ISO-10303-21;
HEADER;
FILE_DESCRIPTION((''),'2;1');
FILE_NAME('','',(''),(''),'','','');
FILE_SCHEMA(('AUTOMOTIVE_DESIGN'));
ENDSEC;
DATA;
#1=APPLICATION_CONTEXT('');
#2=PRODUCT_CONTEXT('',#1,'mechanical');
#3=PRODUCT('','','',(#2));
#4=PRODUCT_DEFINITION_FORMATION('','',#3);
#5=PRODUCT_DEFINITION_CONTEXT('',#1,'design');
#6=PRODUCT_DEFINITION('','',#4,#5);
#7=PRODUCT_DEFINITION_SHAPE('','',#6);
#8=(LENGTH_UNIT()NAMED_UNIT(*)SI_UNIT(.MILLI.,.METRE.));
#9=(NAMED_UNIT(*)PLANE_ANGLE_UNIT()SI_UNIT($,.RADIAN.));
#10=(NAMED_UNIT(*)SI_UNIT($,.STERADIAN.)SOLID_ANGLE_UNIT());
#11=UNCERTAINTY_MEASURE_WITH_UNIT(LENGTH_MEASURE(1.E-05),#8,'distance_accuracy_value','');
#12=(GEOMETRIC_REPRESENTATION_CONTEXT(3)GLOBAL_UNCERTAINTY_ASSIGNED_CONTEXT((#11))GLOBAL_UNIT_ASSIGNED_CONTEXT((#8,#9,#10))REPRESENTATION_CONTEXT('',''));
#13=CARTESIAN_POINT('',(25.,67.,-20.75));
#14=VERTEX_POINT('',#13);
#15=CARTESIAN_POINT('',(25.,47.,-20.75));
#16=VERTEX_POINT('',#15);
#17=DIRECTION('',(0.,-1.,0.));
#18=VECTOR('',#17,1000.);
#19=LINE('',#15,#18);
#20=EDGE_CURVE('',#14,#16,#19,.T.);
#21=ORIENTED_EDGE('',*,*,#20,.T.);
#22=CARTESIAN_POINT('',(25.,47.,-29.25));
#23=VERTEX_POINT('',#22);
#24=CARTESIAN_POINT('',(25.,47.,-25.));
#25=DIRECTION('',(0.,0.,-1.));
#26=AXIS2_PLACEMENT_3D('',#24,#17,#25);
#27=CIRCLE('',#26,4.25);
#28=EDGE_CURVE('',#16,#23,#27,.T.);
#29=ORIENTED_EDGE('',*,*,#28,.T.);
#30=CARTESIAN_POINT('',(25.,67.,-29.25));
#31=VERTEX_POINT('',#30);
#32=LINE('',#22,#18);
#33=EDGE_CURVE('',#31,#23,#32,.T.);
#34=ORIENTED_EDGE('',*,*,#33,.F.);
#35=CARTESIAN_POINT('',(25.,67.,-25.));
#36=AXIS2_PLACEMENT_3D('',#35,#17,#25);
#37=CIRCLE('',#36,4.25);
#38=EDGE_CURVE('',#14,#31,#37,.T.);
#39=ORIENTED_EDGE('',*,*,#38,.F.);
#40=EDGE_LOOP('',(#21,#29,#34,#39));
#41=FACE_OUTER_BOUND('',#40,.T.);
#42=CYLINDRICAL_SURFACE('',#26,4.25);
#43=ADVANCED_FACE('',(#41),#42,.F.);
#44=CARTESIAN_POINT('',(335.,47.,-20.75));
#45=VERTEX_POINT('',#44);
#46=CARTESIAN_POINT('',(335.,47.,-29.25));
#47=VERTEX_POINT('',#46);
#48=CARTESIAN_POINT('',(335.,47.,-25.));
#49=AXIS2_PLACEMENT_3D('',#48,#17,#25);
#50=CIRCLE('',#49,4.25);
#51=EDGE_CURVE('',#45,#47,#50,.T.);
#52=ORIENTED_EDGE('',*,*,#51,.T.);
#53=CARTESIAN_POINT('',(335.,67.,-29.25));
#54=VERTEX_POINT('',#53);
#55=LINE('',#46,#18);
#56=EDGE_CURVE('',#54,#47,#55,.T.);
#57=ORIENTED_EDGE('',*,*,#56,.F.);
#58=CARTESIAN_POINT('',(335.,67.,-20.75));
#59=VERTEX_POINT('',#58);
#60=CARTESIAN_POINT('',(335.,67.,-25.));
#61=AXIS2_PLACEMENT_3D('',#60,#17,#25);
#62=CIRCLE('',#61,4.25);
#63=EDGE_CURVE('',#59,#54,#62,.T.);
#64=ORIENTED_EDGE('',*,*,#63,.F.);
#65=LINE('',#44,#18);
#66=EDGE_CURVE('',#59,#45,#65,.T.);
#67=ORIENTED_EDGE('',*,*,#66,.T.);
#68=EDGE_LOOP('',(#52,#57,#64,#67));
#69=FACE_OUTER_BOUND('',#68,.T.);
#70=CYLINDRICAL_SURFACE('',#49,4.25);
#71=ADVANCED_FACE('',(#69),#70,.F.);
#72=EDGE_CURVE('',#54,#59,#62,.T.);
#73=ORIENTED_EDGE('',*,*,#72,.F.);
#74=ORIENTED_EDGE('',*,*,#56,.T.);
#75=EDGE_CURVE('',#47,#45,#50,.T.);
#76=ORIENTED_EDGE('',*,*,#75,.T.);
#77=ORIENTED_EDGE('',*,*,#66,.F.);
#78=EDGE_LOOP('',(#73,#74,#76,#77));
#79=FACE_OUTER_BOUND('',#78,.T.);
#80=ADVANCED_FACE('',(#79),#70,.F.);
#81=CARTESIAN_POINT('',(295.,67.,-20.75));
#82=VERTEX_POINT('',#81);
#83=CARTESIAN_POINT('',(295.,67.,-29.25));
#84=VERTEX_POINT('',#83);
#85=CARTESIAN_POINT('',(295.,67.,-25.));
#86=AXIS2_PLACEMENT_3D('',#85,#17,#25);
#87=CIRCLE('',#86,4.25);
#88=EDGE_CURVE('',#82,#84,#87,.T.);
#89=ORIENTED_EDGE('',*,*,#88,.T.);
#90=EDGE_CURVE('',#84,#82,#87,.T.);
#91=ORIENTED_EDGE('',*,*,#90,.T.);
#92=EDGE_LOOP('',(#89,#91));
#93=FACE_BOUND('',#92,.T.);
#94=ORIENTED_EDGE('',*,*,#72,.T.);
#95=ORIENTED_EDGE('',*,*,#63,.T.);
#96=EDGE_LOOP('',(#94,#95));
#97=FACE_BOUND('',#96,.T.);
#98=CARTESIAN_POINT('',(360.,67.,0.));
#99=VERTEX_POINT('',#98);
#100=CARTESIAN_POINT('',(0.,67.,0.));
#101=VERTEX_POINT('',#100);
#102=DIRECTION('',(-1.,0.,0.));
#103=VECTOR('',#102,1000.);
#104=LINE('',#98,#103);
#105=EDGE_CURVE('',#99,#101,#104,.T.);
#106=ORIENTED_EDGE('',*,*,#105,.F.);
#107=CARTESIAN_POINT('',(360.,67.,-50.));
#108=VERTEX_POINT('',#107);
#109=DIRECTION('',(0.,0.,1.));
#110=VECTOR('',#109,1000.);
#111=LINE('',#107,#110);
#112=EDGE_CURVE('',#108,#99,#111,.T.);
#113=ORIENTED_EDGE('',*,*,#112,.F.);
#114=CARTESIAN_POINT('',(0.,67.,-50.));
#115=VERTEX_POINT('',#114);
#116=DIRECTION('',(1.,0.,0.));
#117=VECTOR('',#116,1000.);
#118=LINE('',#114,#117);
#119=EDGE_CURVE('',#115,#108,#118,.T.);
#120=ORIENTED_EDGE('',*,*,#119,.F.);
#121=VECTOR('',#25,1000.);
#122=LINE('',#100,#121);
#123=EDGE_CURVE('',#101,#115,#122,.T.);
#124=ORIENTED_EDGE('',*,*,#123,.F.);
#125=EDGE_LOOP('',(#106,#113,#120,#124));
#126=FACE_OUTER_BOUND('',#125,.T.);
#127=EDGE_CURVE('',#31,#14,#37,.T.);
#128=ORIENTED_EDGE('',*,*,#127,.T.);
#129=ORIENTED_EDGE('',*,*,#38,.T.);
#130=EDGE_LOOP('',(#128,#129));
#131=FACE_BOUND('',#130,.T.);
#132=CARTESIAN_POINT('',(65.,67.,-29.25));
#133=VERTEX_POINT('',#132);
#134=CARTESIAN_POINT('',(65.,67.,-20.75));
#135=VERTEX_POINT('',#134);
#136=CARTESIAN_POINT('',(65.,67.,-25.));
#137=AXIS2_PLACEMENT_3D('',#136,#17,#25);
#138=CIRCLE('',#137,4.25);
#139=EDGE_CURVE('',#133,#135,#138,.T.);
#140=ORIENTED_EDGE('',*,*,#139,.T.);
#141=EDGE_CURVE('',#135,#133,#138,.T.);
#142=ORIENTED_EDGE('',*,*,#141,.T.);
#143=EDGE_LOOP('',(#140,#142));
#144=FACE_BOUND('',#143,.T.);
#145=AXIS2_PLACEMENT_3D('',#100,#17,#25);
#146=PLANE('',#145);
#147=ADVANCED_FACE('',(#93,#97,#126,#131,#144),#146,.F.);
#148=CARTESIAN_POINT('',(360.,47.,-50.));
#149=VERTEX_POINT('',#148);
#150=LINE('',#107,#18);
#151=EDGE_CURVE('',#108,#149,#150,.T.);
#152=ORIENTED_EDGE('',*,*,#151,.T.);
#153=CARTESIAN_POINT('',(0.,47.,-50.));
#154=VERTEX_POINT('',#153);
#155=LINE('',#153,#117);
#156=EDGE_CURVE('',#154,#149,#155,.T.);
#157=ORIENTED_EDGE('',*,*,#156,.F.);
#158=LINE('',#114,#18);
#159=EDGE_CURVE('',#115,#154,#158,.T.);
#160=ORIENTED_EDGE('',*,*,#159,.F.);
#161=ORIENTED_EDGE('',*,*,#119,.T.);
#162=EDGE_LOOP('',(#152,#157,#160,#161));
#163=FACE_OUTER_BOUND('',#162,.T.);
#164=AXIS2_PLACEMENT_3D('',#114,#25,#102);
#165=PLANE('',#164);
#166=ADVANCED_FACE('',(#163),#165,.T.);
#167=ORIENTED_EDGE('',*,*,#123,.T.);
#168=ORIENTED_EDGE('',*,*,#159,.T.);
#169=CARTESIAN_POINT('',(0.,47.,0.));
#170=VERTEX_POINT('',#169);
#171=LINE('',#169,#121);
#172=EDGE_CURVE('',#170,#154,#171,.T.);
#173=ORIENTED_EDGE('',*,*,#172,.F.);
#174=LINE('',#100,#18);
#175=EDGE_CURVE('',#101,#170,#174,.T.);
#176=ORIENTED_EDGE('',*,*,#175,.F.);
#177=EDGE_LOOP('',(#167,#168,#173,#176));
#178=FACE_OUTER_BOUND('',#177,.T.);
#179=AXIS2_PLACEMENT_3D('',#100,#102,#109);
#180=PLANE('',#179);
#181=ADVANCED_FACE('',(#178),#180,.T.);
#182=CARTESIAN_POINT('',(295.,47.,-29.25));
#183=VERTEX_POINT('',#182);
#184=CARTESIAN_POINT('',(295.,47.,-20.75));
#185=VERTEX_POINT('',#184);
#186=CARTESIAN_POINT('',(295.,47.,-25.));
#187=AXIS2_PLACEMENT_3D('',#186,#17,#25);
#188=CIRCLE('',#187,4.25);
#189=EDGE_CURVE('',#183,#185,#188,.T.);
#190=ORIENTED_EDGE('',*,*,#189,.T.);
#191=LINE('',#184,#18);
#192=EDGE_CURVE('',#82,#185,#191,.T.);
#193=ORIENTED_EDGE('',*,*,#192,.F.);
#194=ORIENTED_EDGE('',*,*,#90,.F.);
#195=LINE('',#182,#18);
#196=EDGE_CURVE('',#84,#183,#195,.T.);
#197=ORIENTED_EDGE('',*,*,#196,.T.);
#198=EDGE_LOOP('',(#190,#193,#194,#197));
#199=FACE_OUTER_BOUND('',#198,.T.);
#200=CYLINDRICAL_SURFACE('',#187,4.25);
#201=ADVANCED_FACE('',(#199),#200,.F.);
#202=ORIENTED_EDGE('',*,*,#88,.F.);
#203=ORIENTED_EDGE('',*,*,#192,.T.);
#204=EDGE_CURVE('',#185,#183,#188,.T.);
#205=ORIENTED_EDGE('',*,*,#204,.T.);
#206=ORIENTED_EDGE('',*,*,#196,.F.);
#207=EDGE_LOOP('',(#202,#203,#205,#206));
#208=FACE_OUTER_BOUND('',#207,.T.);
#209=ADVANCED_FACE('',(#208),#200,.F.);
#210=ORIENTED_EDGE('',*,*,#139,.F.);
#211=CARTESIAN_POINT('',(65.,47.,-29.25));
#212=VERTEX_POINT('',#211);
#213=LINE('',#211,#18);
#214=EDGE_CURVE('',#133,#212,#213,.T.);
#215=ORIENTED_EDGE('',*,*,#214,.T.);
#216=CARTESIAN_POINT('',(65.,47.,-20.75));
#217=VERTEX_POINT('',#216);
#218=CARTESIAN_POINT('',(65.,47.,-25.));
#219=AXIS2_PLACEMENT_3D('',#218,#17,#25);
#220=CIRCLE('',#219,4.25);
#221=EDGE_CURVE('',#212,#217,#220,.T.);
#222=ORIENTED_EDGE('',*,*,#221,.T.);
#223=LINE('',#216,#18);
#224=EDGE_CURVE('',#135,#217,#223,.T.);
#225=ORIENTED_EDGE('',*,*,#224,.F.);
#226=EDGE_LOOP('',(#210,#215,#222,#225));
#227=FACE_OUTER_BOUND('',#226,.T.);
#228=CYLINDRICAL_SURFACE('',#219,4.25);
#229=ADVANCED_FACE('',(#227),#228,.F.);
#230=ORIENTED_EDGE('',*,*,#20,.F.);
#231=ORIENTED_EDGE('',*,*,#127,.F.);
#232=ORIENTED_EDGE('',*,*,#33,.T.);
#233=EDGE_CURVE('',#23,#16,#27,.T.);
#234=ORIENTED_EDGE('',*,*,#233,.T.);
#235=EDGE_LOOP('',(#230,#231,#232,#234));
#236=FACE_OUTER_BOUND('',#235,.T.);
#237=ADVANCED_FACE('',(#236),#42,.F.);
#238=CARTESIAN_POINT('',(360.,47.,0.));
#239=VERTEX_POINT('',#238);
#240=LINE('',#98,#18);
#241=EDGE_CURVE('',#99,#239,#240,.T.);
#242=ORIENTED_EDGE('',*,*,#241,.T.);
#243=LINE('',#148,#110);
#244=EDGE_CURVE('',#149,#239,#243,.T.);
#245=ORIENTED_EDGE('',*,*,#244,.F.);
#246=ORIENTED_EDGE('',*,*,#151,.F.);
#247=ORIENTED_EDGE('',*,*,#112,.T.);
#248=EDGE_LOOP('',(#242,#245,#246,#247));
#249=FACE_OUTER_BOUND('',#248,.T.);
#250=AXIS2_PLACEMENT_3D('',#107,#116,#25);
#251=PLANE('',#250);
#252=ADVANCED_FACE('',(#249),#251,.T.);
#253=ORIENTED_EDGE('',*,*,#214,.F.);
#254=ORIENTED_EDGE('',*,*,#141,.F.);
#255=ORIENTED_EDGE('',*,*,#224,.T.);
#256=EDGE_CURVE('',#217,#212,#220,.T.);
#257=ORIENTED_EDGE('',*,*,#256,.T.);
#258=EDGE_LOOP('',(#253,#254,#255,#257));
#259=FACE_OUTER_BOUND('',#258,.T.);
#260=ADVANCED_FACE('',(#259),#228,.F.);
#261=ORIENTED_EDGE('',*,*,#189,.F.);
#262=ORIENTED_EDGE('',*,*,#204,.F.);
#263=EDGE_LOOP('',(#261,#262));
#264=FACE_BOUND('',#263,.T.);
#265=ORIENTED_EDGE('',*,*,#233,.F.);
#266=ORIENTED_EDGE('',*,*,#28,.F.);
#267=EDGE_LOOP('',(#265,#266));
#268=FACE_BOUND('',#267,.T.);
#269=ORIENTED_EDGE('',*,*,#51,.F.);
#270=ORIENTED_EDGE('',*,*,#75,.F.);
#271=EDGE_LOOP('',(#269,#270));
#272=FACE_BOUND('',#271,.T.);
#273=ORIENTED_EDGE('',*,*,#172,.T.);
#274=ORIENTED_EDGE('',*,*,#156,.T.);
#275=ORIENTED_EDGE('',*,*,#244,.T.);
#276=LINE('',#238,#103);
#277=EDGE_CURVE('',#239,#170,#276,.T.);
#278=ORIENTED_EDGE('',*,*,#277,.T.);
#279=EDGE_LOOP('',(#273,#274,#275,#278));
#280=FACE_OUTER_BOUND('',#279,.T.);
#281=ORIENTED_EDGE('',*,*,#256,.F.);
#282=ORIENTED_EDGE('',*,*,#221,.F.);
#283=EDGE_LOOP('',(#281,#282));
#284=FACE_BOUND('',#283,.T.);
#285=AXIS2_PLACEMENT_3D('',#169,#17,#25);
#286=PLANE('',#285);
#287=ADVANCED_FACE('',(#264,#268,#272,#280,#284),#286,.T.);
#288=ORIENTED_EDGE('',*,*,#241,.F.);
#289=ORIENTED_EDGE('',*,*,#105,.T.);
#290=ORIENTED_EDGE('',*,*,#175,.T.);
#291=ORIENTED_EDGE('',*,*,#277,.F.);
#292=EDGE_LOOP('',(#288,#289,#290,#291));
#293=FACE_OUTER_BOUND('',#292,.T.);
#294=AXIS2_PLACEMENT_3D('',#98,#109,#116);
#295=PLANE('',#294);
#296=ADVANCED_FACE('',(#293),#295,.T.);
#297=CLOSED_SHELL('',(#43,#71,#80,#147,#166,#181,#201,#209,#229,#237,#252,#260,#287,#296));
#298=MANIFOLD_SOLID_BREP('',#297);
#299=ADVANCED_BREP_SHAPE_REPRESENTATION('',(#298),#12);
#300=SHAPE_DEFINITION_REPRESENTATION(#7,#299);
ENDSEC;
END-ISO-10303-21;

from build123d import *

# Parameters (mm, degrees)
SKETCH_1_W          = 360
SKETCH_1_H          = 50
SKETCH_1_R          = 2.5
EXTRUDE_1_DEPTH     = 20
HOLE_WIZARD_M10_1_D = 8.5


with BuildPart() as part:
    # 草图1 → 凸台-拉伸1 (new body)
    with BuildSketch(Plane.XZ.offset(-47)):
        with Locations((180, -25)):
            Rectangle(SKETCH_1_W, SKETCH_1_H)
        with Locations(Location((335, -25, 0), (0, 0, 90))):
            Circle(SKETCH_1_R, mode=Mode.SUBTRACT)
        with Locations(Location((65, -25, 0), (0, 0, 90))):
            Circle(SKETCH_1_R, mode=Mode.SUBTRACT)
        with Locations(Location((25, -25, 0), (0, 0, 90))):
            Circle(SKETCH_1_R, mode=Mode.SUBTRACT)
        with Locations(Location((295, -25, 0), (0, 0, 90))):
            Circle(SKETCH_1_R, mode=Mode.SUBTRACT)
    extrude(amount=-EXTRUDE_1_DEPTH)

    # M10 螺纹孔1 (through all)
    with Locations(Plane(origin=(0, 47, 0), x_dir=(-1, 0, 0), z_dir=(0, -1, 0))):
        with Locations((-335, 25), (-295, 25), (-65, 25), (-25, 25)):
            Hole(HOLE_WIZARD_M10_1_D / 2)


solid = part.part
